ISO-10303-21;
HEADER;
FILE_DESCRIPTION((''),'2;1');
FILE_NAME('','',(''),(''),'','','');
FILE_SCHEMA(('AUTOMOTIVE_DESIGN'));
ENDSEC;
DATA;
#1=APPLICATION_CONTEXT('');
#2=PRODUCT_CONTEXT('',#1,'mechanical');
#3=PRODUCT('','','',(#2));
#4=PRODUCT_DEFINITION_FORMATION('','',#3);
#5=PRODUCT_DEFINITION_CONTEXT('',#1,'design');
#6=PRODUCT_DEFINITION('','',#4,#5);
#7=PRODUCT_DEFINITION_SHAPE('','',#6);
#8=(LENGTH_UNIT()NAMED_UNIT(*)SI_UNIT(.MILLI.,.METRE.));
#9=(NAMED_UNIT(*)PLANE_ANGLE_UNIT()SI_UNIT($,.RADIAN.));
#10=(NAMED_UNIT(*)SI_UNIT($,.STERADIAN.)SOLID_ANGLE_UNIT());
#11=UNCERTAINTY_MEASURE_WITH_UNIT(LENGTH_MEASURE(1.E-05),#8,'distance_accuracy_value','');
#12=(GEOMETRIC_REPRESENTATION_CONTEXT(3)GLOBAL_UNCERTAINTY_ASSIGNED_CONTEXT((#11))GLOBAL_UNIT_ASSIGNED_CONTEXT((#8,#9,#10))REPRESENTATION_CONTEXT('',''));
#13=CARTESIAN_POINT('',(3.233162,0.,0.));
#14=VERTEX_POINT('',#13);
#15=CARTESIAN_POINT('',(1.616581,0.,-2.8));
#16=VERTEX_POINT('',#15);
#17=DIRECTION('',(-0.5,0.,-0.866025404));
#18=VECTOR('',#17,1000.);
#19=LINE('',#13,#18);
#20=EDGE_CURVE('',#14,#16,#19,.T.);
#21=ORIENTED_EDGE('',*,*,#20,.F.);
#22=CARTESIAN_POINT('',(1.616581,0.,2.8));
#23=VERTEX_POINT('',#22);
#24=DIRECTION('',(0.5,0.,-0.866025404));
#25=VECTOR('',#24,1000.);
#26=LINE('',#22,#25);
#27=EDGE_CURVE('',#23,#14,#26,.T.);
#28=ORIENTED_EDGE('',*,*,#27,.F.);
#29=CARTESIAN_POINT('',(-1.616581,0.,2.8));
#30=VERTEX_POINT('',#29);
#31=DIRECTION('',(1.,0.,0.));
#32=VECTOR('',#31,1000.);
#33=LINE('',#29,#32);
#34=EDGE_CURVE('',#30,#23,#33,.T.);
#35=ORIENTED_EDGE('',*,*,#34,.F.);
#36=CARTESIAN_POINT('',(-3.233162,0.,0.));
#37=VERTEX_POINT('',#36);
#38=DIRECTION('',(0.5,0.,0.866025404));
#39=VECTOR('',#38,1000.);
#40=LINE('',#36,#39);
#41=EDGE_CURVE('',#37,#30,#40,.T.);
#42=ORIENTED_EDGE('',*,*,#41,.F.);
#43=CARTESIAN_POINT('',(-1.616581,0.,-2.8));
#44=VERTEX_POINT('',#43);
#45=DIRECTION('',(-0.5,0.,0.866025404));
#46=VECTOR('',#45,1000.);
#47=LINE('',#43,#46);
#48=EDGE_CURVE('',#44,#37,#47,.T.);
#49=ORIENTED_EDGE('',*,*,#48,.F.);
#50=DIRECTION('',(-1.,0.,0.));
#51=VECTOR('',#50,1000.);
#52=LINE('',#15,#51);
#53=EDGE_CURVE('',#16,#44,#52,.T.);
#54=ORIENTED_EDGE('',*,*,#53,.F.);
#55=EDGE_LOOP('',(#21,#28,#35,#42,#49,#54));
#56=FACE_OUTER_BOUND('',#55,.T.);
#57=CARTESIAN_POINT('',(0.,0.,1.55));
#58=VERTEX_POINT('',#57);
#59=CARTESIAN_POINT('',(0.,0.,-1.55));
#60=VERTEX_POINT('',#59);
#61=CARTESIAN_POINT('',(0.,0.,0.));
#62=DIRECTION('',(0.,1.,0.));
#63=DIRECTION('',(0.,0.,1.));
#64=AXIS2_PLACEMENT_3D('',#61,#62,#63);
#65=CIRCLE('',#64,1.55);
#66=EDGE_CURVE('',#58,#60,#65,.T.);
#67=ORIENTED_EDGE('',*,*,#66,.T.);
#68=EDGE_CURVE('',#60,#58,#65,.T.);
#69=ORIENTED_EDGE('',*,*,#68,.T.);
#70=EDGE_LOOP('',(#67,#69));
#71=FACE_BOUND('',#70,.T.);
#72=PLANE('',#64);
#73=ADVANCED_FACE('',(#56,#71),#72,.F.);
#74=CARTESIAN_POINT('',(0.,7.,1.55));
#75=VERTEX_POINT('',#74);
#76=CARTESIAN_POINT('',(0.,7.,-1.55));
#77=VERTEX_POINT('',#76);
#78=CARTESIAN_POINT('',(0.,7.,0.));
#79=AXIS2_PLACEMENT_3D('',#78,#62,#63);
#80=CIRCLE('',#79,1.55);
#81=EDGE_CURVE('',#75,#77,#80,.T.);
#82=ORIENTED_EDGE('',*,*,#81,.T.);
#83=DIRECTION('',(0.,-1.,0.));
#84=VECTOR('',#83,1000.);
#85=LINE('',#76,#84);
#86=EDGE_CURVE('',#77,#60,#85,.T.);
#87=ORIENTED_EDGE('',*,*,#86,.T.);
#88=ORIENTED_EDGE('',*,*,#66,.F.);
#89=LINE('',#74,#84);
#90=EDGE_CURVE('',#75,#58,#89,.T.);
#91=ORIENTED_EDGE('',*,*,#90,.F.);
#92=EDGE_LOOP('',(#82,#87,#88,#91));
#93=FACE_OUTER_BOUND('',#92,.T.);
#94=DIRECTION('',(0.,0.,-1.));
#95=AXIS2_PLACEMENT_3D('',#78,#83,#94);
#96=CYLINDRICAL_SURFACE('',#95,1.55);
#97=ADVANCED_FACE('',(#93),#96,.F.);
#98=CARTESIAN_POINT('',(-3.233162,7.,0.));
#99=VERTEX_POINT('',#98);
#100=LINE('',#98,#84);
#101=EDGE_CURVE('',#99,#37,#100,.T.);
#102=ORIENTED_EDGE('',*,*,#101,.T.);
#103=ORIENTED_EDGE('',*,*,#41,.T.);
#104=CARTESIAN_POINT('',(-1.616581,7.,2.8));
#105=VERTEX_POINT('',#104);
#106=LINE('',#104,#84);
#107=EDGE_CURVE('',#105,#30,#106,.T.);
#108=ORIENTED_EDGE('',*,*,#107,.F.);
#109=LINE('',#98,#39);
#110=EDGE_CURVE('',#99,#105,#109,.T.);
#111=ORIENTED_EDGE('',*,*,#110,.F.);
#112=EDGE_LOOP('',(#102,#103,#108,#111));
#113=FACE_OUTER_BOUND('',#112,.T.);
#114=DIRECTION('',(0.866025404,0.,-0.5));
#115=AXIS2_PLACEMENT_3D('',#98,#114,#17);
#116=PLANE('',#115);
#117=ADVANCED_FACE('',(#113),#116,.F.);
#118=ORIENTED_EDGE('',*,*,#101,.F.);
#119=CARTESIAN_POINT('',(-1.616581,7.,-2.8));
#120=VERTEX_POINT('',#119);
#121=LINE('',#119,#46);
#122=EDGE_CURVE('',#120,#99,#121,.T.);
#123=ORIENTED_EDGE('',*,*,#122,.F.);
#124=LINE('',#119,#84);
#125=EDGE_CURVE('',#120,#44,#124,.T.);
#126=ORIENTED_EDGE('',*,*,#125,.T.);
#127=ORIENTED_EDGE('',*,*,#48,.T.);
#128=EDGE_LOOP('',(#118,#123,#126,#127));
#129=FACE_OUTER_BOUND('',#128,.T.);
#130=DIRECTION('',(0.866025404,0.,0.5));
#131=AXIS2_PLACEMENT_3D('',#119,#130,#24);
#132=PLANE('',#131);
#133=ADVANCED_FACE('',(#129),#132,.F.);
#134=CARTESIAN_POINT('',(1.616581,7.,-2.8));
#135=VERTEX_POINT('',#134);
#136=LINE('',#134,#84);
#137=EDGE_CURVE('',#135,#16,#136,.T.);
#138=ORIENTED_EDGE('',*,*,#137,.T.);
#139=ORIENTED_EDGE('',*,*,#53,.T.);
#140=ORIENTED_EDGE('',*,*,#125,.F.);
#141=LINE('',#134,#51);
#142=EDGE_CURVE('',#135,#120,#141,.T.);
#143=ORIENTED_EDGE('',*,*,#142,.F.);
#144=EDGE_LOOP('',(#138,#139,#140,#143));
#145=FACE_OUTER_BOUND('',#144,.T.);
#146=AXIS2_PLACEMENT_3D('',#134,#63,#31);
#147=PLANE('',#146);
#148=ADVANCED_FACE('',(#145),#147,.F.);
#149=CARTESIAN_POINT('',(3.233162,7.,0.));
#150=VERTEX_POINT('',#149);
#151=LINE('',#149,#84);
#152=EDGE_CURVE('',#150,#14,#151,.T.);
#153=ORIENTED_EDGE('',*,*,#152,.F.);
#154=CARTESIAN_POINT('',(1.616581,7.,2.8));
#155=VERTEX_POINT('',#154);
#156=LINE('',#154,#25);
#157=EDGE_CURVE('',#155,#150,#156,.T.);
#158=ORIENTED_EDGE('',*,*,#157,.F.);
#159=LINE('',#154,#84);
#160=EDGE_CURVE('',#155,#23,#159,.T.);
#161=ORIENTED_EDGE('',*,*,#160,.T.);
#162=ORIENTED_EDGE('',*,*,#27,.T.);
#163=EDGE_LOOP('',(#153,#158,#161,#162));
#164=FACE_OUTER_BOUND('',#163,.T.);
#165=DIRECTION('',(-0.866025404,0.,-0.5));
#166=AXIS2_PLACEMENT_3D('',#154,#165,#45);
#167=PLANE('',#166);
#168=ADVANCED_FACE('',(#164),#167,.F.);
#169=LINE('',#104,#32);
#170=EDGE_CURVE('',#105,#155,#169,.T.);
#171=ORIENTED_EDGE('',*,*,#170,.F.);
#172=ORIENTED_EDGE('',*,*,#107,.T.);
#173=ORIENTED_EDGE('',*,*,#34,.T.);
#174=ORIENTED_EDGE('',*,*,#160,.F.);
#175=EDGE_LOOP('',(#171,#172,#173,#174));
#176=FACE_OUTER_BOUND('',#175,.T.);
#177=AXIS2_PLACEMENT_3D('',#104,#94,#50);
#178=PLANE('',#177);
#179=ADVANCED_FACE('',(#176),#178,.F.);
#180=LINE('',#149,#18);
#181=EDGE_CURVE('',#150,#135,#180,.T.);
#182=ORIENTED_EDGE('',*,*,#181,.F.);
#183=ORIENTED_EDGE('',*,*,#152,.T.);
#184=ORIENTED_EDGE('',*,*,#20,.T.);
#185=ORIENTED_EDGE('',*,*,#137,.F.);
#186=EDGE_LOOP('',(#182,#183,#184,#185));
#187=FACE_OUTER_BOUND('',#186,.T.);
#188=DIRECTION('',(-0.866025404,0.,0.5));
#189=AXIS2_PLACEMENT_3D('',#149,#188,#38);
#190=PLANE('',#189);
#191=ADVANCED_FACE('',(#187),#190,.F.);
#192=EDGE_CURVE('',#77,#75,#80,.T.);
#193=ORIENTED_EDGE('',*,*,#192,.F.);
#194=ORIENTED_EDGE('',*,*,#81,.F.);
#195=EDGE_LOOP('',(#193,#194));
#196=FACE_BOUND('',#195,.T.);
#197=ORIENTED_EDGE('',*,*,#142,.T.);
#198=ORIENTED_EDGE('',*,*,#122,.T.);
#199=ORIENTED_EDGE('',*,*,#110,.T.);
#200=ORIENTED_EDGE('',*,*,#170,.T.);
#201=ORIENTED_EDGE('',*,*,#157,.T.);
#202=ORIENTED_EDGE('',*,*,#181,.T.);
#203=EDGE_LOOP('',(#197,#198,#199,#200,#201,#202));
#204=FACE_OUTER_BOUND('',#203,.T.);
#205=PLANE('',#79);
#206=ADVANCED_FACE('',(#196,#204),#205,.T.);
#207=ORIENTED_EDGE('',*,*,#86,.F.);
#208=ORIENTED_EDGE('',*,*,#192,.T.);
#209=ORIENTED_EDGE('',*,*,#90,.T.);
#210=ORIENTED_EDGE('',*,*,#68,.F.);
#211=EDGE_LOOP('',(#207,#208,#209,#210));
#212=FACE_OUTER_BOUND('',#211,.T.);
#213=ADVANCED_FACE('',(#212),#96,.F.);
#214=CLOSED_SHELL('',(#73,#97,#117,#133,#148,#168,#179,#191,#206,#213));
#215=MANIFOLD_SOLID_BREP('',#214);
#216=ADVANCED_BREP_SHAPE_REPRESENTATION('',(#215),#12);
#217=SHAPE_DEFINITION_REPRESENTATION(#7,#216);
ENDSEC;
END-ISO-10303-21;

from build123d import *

# Parameters (mm, degrees)
SKETCH_1_R      = 1.55
EXTRUDE_1_DEPTH = 7


with BuildPart() as part:
    # 草图1 → 凸台-拉伸1 (new body)
    with BuildSketch(Plane(origin=(0, 0, 0), x_dir=(1, 0, 0), z_dir=(0, 1, 0))):
        Polygon((1.616580754, -2.8), (3.233161507, 0), (1.616580754, 2.8), (-1.616580754, 2.8), (-3.233161507, 0), (-1.616580754, -2.8), align=None)
        with Locations(Location((0, 0, 0), (0, 0, 270))):
            Circle(SKETCH_1_R, mode=Mode.SUBTRACT)
    extrude(amount=EXTRUDE_1_DEPTH)


solid = part.part
